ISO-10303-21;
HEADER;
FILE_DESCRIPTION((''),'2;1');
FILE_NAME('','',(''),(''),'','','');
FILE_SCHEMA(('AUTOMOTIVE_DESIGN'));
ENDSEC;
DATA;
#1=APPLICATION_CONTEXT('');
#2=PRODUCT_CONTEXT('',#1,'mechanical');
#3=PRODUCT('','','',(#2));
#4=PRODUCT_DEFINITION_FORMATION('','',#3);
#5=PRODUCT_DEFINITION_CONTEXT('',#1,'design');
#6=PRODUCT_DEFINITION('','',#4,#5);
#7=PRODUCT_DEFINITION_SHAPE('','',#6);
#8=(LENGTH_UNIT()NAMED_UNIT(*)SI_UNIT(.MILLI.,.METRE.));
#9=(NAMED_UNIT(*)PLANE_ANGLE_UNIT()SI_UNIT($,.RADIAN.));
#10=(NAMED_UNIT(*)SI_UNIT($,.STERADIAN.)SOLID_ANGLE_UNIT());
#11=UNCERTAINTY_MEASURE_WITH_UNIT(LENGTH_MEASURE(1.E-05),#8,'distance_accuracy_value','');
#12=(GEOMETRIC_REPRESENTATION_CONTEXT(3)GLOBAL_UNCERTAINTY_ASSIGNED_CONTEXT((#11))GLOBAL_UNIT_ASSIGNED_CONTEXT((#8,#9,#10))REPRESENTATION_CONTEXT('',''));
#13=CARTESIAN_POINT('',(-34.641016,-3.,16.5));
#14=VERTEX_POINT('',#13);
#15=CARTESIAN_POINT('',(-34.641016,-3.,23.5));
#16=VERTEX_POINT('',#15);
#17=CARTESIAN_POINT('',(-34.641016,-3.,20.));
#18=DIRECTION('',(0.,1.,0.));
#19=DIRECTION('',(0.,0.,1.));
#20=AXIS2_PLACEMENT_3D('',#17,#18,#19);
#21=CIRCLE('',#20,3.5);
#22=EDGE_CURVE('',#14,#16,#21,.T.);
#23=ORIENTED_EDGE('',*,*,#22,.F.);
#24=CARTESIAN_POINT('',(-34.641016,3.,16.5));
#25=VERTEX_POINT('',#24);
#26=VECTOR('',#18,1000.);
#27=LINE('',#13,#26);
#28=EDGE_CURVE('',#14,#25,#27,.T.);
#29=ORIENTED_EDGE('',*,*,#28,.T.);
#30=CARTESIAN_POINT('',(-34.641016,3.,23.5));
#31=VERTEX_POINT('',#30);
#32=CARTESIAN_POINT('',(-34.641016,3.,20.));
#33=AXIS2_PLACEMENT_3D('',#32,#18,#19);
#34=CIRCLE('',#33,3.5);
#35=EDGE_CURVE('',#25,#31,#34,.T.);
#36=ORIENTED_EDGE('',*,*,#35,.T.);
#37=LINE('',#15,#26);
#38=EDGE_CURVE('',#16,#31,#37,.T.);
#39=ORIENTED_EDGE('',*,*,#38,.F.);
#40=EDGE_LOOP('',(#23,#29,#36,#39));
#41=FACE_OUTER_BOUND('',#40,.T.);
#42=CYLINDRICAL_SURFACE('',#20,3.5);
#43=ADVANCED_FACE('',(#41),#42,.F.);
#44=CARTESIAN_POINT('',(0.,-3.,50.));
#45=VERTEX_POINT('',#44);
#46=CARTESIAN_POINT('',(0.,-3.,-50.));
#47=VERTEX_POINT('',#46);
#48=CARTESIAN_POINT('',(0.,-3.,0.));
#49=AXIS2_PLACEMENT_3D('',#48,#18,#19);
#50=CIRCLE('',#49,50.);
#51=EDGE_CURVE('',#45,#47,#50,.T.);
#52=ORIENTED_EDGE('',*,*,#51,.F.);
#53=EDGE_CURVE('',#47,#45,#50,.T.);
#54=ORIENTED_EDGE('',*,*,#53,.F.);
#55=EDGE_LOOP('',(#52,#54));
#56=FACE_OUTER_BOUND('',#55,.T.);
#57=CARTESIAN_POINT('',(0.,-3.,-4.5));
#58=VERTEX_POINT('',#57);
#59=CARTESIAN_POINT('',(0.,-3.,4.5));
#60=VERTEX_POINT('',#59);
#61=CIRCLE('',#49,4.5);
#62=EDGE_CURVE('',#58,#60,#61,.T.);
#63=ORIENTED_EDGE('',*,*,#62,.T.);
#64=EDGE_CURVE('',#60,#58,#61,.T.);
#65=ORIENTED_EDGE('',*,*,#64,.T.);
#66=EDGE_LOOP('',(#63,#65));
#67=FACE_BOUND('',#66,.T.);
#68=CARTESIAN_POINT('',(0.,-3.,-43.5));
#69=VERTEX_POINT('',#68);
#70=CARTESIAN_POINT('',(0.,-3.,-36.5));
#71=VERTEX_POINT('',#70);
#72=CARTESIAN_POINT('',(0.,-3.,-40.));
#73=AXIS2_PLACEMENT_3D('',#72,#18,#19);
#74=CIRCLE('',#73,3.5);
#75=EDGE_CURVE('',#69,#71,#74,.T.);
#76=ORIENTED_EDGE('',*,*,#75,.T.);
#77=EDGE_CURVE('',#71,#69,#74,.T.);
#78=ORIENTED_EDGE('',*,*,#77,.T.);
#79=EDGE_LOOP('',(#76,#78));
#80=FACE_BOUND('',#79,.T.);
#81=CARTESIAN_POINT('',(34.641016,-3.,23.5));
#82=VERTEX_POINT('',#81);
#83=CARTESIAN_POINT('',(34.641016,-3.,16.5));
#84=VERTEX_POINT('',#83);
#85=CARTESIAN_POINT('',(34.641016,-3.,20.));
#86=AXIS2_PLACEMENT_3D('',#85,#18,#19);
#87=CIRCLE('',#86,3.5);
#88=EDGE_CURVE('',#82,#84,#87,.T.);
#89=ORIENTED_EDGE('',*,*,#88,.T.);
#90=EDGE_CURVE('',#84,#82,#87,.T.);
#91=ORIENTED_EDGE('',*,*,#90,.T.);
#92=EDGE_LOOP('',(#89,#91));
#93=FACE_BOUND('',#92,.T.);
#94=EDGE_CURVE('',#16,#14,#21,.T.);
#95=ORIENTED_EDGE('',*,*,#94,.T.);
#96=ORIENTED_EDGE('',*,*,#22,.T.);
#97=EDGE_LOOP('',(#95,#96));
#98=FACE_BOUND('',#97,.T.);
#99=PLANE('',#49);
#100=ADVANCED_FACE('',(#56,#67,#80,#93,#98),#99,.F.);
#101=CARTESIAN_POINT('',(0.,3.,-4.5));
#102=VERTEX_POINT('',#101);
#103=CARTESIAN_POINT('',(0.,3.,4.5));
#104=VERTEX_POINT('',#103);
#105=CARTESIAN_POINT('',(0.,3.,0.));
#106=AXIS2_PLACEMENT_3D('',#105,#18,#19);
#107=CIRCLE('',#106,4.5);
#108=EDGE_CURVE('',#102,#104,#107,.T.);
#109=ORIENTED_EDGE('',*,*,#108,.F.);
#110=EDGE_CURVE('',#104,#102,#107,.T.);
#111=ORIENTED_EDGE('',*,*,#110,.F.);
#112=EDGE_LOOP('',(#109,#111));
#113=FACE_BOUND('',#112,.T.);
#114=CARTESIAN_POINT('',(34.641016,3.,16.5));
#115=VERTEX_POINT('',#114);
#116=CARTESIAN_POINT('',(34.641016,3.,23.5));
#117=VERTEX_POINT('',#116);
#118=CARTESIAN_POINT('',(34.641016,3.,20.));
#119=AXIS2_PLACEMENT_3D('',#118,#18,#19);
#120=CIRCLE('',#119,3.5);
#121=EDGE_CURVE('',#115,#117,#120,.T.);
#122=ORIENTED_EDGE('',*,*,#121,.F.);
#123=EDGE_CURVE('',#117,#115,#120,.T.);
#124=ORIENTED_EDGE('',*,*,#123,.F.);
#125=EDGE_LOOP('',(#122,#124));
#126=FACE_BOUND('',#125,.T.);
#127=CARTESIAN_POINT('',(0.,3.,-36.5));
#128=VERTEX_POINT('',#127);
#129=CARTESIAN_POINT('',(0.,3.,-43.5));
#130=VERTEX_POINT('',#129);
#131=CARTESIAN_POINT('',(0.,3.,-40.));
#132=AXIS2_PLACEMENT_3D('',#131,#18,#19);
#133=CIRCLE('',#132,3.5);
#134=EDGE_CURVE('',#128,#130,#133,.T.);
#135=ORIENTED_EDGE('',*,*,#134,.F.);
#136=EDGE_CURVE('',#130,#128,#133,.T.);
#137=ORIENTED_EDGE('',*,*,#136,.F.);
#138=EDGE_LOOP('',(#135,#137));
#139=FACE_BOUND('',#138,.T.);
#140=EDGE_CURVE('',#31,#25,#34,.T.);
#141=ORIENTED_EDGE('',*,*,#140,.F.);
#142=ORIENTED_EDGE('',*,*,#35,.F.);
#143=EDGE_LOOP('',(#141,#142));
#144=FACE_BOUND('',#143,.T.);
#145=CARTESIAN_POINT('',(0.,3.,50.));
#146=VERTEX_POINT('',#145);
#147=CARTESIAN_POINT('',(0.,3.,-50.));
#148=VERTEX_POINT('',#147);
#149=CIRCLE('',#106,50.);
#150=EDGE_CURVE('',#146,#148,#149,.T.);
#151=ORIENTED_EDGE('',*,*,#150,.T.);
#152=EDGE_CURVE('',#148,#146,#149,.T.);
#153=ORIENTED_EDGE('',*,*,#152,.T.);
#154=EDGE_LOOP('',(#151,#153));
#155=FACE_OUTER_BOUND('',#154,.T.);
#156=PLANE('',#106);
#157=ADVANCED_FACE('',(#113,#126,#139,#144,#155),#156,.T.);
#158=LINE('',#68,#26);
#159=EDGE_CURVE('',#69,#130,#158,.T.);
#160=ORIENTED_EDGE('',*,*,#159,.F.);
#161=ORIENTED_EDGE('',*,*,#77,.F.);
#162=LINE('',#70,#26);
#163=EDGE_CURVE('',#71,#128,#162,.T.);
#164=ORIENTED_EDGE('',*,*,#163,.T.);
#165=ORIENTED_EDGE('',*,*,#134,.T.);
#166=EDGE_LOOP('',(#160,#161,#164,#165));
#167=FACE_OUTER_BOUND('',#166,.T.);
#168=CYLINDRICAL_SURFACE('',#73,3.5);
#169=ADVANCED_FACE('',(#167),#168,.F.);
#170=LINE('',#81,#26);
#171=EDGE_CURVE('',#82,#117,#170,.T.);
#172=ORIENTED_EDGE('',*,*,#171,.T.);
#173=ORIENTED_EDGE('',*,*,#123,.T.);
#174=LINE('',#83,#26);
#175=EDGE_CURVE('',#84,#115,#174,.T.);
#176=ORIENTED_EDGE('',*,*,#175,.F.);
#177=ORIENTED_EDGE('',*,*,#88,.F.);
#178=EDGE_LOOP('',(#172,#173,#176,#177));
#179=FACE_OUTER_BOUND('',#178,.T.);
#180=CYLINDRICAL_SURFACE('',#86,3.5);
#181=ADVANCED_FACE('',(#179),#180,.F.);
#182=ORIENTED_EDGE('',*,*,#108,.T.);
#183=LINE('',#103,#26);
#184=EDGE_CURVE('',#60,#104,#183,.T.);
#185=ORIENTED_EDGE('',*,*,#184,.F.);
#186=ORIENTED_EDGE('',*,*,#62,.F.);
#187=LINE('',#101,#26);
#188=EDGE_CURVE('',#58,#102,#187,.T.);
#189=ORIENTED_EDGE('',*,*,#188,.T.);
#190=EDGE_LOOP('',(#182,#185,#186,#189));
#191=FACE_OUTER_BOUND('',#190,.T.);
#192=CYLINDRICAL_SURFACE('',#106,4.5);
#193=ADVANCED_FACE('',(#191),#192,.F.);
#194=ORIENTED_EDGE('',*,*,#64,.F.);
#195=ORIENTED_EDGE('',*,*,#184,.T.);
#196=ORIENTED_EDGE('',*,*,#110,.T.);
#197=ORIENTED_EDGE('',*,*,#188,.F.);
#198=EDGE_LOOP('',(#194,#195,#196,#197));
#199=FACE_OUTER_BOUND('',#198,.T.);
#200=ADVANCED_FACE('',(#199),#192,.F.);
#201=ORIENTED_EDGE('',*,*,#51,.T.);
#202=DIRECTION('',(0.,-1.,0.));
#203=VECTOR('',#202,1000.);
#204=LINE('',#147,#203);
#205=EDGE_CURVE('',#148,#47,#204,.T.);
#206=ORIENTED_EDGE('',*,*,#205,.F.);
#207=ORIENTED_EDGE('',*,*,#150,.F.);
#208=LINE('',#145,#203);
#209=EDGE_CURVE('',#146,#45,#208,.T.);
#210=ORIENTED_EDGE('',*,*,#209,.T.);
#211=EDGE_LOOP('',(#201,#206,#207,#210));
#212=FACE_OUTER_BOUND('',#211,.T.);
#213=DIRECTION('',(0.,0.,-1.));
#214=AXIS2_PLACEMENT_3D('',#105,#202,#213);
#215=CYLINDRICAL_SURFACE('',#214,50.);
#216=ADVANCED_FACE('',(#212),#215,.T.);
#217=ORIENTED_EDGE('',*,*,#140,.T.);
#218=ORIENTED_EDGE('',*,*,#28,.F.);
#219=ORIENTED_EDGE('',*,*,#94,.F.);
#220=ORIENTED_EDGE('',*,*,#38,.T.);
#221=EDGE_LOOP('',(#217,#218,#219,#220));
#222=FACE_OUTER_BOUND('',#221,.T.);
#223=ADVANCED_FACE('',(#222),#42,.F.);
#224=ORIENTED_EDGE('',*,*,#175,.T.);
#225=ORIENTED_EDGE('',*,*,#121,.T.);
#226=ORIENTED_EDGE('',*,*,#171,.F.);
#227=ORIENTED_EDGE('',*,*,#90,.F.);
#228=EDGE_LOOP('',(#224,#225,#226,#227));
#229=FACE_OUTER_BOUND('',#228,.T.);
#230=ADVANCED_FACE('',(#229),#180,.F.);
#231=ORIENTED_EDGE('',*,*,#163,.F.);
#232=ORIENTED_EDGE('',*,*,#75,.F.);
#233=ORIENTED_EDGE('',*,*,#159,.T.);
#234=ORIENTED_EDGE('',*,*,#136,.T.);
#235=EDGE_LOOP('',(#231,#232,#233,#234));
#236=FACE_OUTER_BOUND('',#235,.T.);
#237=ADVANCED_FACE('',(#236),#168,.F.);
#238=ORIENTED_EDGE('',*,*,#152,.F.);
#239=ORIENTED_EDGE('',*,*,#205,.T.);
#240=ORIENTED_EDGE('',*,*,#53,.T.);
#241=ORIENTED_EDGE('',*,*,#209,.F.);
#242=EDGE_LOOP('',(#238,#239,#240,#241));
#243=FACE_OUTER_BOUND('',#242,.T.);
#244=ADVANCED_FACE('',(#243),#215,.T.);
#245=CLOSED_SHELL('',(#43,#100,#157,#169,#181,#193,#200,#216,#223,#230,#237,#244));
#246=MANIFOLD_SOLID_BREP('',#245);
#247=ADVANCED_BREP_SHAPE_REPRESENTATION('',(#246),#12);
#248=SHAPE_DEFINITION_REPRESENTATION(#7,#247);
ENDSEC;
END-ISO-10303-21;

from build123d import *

# Parameters (mm, degrees)
SKETCH1_R              = 50
BOSS_EXTRUDE1_DEPTH    = 3
SKETCH2_R              = 3.5
CUT_EXTRUDE1_DEPTH     = 71.964779997
M10X1_0_TAPPED_HOLE1_D = 9


with BuildPart() as part:
    # Sketch1 → Boss-Extrude1 (new, symmetric)
    with BuildSketch(Plane(origin=(0, 0, 0), x_dir=(1, 0, 0), z_dir=(0, 1, 0))):
        with Locations(Location((0, 0, 0), (0, 0, 270))):
            Circle(SKETCH1_R)
    extrude(amount=BOSS_EXTRUDE1_DEPTH, both=True)

    # Sketch2 → Cut-Extrude1 (cut, through all)
    with BuildSketch(Plane(origin=(0, 3, 0), x_dir=(1, 0, 0), z_dir=(0, 1, 0))):
        with Locations(Location((0, 40, 0), (0, 0, 270))):
            Circle(SKETCH2_R)
        with Locations(Location((34.641016151, -20, 0), (0, 0, 270))):
            Circle(SKETCH2_R)
        with Locations(Location((-34.641016151, -20, 0), (0, 0, 270))):
            Circle(SKETCH2_R)
    extrude(amount=-CUT_EXTRUDE1_DEPTH, mode=Mode.SUBTRACT)

    # M10x1.0 Tapped Hole1 (through all)
    with Locations(Plane(origin=(0, 3, 0), x_dir=(1, 0, 0), z_dir=(0, 1, 0))):
        with Locations((0, 0)):
            Hole(M10X1_0_TAPPED_HOLE1_D / 2)


solid = part.part
